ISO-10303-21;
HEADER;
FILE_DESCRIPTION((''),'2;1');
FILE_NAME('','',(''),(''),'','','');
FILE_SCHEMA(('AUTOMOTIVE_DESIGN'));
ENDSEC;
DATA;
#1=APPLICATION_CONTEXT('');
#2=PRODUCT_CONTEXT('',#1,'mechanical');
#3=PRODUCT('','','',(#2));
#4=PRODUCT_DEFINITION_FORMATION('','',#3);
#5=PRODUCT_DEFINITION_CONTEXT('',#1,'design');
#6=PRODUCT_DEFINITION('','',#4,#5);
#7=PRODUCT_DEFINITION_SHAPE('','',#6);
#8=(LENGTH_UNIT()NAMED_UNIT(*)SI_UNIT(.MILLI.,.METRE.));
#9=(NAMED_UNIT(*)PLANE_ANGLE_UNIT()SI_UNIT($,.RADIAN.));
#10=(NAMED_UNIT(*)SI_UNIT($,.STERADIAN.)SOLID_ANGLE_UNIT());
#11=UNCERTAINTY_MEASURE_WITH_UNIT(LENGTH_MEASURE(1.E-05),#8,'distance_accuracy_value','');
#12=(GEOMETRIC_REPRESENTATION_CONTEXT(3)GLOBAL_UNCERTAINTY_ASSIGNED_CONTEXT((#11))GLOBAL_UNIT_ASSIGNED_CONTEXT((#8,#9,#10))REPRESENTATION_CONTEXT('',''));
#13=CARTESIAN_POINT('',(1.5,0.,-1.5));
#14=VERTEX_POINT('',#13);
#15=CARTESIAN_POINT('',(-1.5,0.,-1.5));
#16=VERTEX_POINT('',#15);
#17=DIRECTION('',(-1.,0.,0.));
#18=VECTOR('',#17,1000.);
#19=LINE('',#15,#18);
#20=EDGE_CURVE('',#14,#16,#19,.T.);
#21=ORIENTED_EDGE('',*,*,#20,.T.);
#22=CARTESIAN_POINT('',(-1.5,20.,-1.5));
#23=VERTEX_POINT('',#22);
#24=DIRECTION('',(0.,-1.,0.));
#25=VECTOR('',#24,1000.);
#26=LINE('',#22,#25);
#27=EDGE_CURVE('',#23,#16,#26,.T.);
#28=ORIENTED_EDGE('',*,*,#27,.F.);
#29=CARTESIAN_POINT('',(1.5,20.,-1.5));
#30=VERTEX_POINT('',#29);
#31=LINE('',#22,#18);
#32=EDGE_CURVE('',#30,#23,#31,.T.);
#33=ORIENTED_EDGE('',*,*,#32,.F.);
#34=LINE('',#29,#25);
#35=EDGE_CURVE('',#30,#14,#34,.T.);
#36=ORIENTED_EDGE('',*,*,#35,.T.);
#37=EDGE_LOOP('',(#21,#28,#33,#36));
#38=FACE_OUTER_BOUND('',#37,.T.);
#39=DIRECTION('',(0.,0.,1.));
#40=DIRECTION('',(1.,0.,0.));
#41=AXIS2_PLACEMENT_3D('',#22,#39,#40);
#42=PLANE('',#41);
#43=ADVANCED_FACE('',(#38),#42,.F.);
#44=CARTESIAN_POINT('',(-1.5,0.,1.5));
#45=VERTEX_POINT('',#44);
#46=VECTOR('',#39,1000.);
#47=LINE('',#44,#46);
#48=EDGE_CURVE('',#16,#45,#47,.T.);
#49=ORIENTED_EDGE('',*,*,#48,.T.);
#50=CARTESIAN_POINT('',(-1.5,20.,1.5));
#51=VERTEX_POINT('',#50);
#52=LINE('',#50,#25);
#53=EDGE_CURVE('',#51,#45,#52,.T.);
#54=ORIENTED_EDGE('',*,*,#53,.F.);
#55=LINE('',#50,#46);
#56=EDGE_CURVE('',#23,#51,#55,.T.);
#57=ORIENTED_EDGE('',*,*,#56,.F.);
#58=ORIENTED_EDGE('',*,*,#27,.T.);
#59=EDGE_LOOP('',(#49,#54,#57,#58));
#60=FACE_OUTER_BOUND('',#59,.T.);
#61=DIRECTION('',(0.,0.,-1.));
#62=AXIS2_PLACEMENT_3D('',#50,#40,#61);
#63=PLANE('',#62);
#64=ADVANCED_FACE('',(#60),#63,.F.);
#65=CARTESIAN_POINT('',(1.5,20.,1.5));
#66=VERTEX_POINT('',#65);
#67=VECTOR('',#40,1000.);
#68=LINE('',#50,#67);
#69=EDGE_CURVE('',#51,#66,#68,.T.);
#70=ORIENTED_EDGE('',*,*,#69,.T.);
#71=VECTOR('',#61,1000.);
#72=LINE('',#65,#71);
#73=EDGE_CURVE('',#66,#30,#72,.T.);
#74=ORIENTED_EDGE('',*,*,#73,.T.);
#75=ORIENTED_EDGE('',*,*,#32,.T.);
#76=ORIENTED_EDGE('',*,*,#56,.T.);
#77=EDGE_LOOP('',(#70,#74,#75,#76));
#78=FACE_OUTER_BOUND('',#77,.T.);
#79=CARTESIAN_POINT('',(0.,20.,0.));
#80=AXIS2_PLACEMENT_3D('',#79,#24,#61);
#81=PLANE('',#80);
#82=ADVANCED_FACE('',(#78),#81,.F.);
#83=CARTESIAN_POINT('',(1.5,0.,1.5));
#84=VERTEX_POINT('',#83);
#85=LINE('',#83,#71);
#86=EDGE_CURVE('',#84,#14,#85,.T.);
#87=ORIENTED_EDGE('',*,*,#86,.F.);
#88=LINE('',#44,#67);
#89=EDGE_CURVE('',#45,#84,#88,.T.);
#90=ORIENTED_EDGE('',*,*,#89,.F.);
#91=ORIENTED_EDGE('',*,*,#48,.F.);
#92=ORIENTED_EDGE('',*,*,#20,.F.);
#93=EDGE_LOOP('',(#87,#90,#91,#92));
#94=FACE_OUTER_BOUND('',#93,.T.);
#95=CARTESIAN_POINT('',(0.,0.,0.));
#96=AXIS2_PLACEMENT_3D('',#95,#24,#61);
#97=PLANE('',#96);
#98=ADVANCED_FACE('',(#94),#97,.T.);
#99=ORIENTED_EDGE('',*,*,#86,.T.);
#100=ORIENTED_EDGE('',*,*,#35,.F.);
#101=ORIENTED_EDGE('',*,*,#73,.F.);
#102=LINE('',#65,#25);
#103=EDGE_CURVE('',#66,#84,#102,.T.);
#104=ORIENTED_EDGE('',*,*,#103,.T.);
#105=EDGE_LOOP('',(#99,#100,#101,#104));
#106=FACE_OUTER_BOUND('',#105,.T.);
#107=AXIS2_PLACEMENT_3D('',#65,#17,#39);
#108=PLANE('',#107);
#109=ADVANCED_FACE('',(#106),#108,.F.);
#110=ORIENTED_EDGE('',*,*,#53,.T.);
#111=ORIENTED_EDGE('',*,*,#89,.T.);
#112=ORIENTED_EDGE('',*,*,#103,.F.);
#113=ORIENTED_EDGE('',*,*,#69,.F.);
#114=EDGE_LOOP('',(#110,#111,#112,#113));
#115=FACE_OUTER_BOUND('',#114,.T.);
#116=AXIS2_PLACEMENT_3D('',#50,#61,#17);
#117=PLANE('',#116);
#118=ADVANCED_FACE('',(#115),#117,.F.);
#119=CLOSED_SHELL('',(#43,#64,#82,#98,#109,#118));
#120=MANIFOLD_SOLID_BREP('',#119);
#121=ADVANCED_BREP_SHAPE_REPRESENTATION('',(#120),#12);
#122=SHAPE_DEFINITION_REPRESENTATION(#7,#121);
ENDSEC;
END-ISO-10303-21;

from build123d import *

# Parameters (mm, degrees)
SKETCH1_W           = 3
SKETCH1_H           = 3
BOSS_EXTRUDE1_DEPTH = 20


with BuildPart() as part:
    # Sketch1 → Boss-Extrude1 (new body)
    with BuildSketch(Plane(origin=(0, 0, 0), x_dir=(1, 0, 0), z_dir=(0, 1, 0))):
        Rectangle(SKETCH1_W, SKETCH1_H)
    extrude(amount=BOSS_EXTRUDE1_DEPTH)


solid = part.part
